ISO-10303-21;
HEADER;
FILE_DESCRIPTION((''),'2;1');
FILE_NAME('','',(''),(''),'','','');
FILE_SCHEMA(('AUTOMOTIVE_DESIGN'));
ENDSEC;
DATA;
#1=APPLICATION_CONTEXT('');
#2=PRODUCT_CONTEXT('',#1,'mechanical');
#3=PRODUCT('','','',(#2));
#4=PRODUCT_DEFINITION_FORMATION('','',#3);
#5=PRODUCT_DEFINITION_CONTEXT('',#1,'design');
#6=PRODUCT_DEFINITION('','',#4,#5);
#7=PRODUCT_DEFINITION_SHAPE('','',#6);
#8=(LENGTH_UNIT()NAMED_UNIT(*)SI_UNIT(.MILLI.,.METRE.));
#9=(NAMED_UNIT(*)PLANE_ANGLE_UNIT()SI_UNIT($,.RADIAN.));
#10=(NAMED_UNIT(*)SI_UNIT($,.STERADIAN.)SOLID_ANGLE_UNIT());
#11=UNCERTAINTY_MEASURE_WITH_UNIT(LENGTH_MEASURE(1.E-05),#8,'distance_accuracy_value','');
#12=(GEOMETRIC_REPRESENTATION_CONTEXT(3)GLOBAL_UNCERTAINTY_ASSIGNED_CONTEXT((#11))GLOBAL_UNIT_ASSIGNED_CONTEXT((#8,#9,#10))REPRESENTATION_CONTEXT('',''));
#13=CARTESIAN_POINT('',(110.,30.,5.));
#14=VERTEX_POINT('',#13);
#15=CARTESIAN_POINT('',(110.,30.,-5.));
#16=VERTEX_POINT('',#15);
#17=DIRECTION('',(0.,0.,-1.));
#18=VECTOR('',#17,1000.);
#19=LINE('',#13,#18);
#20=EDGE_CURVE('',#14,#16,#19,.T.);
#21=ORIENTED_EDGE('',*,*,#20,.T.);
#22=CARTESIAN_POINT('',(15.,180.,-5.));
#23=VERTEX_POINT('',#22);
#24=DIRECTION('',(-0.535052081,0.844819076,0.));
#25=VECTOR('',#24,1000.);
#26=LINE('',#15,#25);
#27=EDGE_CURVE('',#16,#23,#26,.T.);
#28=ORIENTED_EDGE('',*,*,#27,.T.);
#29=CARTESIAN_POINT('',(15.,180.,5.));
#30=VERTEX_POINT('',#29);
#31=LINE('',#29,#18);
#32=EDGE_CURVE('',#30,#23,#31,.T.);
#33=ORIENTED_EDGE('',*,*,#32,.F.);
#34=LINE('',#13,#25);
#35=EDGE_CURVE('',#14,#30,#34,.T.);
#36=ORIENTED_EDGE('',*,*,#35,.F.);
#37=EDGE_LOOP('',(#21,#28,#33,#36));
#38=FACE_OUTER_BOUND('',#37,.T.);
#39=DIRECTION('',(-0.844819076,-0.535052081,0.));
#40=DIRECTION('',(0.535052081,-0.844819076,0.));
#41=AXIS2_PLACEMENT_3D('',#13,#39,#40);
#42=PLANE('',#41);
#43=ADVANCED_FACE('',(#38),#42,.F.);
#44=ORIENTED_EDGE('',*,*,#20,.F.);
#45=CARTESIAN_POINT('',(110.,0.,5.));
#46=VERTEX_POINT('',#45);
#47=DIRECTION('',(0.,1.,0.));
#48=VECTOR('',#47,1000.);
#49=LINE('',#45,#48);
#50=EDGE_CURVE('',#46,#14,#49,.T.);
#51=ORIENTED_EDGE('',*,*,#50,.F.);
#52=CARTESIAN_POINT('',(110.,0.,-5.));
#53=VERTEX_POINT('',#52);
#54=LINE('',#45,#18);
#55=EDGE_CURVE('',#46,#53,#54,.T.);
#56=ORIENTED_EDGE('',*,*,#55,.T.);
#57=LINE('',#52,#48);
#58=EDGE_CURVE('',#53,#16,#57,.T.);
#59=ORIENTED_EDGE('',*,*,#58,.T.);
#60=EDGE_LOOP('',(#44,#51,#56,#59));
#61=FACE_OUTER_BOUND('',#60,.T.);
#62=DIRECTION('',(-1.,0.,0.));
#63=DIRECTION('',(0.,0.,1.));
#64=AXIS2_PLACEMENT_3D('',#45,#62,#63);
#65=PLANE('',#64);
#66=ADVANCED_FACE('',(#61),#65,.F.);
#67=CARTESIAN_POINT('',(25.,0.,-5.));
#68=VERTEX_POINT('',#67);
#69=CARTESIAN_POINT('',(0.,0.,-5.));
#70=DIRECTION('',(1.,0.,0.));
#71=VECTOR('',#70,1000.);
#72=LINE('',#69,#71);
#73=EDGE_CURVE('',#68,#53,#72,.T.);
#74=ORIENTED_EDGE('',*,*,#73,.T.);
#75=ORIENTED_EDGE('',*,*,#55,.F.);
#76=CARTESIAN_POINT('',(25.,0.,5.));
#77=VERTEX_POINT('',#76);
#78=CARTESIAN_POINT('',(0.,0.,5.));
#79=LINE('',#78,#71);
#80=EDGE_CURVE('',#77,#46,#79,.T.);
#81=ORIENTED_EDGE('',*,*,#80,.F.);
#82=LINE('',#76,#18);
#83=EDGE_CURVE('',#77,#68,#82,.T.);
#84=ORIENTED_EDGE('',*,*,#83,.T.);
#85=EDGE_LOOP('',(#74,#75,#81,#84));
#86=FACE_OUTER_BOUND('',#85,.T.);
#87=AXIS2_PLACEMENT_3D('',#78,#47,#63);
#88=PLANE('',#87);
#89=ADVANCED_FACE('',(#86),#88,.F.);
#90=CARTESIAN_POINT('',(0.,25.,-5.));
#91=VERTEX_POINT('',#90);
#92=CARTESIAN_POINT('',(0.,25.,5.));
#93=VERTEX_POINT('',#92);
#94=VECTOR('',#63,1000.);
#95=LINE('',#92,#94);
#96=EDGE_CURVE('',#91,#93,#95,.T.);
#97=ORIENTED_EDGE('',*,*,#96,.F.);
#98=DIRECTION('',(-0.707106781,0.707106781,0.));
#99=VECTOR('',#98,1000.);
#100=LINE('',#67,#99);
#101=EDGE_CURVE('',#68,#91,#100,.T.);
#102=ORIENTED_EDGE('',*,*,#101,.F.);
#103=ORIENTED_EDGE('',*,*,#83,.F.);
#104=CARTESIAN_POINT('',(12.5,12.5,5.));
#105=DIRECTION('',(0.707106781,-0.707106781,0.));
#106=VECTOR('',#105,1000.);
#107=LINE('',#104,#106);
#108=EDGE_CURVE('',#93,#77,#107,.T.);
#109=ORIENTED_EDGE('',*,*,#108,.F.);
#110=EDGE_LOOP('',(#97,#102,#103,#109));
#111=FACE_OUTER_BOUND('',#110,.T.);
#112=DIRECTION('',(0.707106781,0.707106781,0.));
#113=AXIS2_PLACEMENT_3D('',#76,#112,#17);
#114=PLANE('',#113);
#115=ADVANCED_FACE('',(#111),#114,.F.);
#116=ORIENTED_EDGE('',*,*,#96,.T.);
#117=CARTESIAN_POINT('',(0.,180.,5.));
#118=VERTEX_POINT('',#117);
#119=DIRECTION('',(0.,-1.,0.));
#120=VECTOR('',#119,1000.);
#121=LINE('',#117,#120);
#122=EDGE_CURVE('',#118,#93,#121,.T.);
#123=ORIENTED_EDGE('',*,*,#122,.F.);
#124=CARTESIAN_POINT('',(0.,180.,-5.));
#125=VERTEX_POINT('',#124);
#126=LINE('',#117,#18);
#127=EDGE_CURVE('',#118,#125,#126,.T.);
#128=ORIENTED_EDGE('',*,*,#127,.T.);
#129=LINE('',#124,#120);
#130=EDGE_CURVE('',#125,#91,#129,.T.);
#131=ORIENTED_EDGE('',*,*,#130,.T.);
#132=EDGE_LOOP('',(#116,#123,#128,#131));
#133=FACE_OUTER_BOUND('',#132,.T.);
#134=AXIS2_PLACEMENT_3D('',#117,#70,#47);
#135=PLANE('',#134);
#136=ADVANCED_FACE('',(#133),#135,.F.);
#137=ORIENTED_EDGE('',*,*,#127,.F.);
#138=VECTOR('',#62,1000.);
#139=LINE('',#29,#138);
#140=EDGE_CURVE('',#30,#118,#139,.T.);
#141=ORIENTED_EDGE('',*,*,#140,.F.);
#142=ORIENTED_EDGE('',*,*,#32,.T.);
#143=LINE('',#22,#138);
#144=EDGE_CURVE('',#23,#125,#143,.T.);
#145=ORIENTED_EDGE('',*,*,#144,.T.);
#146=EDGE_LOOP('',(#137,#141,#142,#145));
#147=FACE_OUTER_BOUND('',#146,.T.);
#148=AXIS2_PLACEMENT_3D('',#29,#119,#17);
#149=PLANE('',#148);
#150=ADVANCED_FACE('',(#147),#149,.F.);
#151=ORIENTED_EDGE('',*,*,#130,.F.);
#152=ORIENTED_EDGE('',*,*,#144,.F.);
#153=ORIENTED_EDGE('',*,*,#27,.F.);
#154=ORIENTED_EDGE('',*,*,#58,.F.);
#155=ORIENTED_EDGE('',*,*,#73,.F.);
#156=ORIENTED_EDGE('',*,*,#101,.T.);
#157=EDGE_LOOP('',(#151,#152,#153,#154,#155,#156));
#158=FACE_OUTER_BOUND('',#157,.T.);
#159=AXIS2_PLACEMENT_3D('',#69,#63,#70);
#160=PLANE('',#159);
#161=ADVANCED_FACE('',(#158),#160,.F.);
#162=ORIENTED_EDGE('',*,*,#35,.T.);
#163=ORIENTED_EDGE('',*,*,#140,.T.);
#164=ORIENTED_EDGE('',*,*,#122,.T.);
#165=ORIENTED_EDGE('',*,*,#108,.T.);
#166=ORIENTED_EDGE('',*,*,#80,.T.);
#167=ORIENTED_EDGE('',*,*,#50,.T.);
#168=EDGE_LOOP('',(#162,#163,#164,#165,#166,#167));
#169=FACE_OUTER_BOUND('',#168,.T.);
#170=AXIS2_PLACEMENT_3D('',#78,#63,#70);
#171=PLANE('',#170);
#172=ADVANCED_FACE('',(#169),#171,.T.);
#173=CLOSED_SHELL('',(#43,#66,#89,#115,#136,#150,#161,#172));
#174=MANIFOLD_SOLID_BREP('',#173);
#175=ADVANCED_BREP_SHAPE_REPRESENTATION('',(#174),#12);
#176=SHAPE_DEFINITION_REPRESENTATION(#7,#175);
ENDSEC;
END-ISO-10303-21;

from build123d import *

# Parameters (mm, degrees)
BOSS_EXTRUDE1_DEPTH = 5
CHAMFER1_SIZE       = 25


with BuildPart() as part:
    # Sketch1 → Boss-Extrude1 (new, symmetric)
    with BuildSketch(Plane.XY):
        Polygon((0, 0), (110, 0), (110, 30), (15, 180), (0, 180), align=None)
    extrude(amount=BOSS_EXTRUDE1_DEPTH, both=True)

    # Chamfer1
    chamfer1_edges = [part.edges().sort_by_distance(p)[0] for p in [
        (0, 0, 0),
    ]]
    chamfer(chamfer1_edges, length=CHAMFER1_SIZE)


solid = part.part
